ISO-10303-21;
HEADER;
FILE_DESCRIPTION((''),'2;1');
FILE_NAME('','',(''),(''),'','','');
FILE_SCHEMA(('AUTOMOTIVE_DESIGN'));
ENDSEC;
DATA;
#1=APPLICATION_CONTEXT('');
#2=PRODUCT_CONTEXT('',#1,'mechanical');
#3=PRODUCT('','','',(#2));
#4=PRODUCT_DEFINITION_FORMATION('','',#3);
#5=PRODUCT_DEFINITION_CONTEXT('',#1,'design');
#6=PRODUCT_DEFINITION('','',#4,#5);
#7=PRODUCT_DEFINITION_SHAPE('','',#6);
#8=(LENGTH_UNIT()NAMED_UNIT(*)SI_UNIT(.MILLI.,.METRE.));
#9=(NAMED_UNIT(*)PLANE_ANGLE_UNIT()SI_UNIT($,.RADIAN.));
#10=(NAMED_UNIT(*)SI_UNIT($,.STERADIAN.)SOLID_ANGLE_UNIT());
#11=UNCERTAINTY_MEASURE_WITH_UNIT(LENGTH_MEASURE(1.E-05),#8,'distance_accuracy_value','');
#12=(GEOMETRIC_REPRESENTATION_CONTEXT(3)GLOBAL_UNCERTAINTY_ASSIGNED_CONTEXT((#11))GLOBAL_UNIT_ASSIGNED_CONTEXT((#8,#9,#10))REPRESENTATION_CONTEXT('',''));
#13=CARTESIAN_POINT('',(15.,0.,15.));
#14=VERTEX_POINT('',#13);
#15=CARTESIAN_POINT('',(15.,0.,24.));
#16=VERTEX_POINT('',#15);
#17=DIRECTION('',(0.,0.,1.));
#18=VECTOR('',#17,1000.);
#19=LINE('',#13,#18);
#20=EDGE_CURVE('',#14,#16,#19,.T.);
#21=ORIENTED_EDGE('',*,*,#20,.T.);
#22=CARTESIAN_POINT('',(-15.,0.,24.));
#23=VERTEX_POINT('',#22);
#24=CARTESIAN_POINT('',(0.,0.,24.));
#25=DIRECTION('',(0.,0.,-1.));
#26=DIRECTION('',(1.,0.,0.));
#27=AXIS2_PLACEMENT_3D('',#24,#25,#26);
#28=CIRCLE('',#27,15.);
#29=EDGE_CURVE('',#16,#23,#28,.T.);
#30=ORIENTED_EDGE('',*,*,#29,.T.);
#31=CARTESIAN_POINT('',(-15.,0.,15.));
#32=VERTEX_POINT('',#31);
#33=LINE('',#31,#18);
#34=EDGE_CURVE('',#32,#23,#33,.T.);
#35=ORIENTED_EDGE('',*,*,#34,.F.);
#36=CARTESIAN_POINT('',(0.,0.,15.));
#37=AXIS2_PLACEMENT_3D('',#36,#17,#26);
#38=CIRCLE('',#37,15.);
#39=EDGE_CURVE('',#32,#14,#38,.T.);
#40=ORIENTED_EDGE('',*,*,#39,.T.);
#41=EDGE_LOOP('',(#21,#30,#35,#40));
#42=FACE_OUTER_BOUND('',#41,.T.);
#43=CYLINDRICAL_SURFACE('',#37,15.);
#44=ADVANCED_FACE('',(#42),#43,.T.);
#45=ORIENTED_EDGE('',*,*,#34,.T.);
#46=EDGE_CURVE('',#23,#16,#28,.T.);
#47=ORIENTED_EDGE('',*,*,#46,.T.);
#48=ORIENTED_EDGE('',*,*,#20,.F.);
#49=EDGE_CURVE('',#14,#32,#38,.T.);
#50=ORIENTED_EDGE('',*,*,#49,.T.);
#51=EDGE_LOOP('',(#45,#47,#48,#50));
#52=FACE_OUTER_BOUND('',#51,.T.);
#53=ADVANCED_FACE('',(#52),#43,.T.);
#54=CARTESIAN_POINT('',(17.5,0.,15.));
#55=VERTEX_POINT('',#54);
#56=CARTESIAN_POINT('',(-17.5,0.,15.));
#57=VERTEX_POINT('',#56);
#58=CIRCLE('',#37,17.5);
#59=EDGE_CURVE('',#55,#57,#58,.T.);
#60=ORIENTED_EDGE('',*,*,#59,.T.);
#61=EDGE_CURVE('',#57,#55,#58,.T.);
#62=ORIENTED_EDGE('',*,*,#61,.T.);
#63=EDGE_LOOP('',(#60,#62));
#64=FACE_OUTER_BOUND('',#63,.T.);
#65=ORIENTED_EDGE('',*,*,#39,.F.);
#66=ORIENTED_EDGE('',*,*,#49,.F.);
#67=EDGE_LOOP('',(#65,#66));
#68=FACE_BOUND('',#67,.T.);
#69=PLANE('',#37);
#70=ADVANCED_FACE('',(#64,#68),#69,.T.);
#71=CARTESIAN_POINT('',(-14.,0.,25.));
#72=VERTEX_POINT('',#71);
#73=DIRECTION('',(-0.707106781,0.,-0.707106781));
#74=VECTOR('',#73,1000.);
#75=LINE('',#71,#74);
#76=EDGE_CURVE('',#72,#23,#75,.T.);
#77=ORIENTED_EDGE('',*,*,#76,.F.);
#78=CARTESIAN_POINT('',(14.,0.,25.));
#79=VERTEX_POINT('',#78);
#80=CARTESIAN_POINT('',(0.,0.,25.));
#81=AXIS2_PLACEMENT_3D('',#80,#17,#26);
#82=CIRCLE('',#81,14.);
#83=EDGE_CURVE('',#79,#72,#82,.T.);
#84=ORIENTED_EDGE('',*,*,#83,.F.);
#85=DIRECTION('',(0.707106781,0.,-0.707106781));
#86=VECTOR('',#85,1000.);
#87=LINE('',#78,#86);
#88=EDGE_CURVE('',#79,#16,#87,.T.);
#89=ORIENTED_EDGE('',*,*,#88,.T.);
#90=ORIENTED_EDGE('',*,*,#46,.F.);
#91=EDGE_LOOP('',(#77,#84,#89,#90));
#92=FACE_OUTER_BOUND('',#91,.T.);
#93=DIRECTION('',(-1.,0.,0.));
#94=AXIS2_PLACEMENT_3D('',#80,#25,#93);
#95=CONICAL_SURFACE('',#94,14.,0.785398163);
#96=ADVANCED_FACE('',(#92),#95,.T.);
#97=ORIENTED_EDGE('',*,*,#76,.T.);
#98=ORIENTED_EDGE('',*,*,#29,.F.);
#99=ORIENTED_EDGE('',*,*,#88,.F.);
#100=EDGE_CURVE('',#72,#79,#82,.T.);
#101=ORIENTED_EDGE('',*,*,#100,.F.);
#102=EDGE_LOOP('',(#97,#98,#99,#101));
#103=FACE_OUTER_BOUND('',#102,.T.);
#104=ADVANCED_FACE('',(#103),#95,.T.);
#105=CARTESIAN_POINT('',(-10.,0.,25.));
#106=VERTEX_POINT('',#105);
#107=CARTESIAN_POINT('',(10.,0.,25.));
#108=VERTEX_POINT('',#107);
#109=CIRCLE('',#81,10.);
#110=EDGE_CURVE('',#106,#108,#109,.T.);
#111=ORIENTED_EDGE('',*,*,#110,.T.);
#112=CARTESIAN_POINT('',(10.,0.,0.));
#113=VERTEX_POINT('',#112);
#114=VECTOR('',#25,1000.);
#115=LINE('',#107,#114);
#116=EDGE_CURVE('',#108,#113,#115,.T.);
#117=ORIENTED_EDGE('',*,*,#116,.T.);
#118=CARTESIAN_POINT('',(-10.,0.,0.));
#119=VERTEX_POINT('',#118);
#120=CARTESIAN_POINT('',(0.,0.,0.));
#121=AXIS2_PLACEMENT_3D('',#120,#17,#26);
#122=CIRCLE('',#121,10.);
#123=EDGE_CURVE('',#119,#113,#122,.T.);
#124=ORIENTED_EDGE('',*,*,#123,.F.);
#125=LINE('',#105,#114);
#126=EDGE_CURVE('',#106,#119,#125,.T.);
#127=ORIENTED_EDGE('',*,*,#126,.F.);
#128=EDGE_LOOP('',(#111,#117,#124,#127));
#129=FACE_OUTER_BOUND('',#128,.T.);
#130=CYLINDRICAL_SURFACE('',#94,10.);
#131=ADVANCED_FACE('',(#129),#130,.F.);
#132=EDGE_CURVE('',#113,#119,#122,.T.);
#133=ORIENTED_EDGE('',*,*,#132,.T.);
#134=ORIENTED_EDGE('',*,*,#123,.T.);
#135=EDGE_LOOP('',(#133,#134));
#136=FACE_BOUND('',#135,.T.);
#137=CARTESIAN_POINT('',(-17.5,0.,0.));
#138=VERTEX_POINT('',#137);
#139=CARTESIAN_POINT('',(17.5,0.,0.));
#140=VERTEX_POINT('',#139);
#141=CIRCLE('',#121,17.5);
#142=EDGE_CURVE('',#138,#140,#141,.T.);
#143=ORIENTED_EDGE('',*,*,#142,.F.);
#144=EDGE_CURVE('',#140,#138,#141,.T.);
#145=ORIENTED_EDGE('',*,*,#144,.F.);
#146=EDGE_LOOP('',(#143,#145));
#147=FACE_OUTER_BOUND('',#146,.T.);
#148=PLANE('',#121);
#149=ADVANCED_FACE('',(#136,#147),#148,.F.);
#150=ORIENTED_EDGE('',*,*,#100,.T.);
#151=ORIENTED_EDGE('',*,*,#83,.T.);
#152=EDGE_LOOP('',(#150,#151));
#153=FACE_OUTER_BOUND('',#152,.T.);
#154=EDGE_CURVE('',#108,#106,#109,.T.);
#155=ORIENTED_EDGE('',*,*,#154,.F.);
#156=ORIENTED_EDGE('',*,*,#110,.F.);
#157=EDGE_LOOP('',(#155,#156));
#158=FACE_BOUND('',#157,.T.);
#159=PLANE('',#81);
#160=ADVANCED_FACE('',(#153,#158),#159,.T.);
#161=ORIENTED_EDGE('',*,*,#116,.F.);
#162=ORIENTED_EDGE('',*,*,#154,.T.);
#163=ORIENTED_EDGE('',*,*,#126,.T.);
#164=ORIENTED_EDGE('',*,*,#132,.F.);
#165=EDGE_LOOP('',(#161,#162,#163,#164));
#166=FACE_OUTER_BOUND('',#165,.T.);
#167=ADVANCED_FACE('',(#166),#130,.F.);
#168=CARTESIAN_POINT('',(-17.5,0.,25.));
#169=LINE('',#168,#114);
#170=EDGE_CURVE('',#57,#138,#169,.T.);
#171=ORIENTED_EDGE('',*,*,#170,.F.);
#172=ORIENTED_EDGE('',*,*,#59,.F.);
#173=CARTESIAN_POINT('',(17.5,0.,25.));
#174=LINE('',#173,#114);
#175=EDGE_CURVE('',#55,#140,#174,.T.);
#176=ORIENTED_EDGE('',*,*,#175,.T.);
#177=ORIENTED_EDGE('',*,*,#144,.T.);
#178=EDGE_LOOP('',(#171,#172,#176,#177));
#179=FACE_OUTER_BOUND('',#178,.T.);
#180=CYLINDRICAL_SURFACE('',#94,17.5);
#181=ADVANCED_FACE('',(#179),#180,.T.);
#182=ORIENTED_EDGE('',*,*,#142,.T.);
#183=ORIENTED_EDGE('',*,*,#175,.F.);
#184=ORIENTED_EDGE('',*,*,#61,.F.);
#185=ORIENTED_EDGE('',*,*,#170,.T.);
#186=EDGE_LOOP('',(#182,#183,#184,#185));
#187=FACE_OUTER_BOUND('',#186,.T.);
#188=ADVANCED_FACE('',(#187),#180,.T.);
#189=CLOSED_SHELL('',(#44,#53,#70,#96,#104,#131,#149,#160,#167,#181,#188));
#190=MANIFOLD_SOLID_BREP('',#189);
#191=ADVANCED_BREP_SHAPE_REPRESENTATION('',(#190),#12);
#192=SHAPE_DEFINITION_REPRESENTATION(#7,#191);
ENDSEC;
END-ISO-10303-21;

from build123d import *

# Parameters (mm, degrees)
SKETCH1_R           = 17.5
SKETCH1_R_2         = 10
BOSS_EXTRUDE1_DEPTH = 25
CUT_EXTRUDE1_START  = -10
SKETCH2_R           = 17.5
SKETCH2_R_2         = 15
CUT_EXTRUDE1_DEPTH  = 10
CHAMFER1_SIZE       = 1


with BuildPart() as part:
    # Sketch1 → Boss-Extrude1 (new body)
    with BuildSketch(Plane.XY):
        Circle(SKETCH1_R)
        Circle(SKETCH1_R_2, mode=Mode.SUBTRACT)
    extrude(amount=BOSS_EXTRUDE1_DEPTH)

    # Sketch2 → Cut-Extrude1 (cut)
    with BuildSketch(Plane.XY.offset(25).offset(CUT_EXTRUDE1_START)):
        Circle(SKETCH2_R)
        Circle(SKETCH2_R_2, mode=Mode.SUBTRACT)
    extrude(amount=CUT_EXTRUDE1_DEPTH, mode=Mode.SUBTRACT)

    # Chamfer1
    chamfer1_edges = [part.edges().sort_by_distance(p)[0] for p in [
        (-15, 0, 25),
    ]]
    chamfer(chamfer1_edges, length=CHAMFER1_SIZE)


solid = part.part
